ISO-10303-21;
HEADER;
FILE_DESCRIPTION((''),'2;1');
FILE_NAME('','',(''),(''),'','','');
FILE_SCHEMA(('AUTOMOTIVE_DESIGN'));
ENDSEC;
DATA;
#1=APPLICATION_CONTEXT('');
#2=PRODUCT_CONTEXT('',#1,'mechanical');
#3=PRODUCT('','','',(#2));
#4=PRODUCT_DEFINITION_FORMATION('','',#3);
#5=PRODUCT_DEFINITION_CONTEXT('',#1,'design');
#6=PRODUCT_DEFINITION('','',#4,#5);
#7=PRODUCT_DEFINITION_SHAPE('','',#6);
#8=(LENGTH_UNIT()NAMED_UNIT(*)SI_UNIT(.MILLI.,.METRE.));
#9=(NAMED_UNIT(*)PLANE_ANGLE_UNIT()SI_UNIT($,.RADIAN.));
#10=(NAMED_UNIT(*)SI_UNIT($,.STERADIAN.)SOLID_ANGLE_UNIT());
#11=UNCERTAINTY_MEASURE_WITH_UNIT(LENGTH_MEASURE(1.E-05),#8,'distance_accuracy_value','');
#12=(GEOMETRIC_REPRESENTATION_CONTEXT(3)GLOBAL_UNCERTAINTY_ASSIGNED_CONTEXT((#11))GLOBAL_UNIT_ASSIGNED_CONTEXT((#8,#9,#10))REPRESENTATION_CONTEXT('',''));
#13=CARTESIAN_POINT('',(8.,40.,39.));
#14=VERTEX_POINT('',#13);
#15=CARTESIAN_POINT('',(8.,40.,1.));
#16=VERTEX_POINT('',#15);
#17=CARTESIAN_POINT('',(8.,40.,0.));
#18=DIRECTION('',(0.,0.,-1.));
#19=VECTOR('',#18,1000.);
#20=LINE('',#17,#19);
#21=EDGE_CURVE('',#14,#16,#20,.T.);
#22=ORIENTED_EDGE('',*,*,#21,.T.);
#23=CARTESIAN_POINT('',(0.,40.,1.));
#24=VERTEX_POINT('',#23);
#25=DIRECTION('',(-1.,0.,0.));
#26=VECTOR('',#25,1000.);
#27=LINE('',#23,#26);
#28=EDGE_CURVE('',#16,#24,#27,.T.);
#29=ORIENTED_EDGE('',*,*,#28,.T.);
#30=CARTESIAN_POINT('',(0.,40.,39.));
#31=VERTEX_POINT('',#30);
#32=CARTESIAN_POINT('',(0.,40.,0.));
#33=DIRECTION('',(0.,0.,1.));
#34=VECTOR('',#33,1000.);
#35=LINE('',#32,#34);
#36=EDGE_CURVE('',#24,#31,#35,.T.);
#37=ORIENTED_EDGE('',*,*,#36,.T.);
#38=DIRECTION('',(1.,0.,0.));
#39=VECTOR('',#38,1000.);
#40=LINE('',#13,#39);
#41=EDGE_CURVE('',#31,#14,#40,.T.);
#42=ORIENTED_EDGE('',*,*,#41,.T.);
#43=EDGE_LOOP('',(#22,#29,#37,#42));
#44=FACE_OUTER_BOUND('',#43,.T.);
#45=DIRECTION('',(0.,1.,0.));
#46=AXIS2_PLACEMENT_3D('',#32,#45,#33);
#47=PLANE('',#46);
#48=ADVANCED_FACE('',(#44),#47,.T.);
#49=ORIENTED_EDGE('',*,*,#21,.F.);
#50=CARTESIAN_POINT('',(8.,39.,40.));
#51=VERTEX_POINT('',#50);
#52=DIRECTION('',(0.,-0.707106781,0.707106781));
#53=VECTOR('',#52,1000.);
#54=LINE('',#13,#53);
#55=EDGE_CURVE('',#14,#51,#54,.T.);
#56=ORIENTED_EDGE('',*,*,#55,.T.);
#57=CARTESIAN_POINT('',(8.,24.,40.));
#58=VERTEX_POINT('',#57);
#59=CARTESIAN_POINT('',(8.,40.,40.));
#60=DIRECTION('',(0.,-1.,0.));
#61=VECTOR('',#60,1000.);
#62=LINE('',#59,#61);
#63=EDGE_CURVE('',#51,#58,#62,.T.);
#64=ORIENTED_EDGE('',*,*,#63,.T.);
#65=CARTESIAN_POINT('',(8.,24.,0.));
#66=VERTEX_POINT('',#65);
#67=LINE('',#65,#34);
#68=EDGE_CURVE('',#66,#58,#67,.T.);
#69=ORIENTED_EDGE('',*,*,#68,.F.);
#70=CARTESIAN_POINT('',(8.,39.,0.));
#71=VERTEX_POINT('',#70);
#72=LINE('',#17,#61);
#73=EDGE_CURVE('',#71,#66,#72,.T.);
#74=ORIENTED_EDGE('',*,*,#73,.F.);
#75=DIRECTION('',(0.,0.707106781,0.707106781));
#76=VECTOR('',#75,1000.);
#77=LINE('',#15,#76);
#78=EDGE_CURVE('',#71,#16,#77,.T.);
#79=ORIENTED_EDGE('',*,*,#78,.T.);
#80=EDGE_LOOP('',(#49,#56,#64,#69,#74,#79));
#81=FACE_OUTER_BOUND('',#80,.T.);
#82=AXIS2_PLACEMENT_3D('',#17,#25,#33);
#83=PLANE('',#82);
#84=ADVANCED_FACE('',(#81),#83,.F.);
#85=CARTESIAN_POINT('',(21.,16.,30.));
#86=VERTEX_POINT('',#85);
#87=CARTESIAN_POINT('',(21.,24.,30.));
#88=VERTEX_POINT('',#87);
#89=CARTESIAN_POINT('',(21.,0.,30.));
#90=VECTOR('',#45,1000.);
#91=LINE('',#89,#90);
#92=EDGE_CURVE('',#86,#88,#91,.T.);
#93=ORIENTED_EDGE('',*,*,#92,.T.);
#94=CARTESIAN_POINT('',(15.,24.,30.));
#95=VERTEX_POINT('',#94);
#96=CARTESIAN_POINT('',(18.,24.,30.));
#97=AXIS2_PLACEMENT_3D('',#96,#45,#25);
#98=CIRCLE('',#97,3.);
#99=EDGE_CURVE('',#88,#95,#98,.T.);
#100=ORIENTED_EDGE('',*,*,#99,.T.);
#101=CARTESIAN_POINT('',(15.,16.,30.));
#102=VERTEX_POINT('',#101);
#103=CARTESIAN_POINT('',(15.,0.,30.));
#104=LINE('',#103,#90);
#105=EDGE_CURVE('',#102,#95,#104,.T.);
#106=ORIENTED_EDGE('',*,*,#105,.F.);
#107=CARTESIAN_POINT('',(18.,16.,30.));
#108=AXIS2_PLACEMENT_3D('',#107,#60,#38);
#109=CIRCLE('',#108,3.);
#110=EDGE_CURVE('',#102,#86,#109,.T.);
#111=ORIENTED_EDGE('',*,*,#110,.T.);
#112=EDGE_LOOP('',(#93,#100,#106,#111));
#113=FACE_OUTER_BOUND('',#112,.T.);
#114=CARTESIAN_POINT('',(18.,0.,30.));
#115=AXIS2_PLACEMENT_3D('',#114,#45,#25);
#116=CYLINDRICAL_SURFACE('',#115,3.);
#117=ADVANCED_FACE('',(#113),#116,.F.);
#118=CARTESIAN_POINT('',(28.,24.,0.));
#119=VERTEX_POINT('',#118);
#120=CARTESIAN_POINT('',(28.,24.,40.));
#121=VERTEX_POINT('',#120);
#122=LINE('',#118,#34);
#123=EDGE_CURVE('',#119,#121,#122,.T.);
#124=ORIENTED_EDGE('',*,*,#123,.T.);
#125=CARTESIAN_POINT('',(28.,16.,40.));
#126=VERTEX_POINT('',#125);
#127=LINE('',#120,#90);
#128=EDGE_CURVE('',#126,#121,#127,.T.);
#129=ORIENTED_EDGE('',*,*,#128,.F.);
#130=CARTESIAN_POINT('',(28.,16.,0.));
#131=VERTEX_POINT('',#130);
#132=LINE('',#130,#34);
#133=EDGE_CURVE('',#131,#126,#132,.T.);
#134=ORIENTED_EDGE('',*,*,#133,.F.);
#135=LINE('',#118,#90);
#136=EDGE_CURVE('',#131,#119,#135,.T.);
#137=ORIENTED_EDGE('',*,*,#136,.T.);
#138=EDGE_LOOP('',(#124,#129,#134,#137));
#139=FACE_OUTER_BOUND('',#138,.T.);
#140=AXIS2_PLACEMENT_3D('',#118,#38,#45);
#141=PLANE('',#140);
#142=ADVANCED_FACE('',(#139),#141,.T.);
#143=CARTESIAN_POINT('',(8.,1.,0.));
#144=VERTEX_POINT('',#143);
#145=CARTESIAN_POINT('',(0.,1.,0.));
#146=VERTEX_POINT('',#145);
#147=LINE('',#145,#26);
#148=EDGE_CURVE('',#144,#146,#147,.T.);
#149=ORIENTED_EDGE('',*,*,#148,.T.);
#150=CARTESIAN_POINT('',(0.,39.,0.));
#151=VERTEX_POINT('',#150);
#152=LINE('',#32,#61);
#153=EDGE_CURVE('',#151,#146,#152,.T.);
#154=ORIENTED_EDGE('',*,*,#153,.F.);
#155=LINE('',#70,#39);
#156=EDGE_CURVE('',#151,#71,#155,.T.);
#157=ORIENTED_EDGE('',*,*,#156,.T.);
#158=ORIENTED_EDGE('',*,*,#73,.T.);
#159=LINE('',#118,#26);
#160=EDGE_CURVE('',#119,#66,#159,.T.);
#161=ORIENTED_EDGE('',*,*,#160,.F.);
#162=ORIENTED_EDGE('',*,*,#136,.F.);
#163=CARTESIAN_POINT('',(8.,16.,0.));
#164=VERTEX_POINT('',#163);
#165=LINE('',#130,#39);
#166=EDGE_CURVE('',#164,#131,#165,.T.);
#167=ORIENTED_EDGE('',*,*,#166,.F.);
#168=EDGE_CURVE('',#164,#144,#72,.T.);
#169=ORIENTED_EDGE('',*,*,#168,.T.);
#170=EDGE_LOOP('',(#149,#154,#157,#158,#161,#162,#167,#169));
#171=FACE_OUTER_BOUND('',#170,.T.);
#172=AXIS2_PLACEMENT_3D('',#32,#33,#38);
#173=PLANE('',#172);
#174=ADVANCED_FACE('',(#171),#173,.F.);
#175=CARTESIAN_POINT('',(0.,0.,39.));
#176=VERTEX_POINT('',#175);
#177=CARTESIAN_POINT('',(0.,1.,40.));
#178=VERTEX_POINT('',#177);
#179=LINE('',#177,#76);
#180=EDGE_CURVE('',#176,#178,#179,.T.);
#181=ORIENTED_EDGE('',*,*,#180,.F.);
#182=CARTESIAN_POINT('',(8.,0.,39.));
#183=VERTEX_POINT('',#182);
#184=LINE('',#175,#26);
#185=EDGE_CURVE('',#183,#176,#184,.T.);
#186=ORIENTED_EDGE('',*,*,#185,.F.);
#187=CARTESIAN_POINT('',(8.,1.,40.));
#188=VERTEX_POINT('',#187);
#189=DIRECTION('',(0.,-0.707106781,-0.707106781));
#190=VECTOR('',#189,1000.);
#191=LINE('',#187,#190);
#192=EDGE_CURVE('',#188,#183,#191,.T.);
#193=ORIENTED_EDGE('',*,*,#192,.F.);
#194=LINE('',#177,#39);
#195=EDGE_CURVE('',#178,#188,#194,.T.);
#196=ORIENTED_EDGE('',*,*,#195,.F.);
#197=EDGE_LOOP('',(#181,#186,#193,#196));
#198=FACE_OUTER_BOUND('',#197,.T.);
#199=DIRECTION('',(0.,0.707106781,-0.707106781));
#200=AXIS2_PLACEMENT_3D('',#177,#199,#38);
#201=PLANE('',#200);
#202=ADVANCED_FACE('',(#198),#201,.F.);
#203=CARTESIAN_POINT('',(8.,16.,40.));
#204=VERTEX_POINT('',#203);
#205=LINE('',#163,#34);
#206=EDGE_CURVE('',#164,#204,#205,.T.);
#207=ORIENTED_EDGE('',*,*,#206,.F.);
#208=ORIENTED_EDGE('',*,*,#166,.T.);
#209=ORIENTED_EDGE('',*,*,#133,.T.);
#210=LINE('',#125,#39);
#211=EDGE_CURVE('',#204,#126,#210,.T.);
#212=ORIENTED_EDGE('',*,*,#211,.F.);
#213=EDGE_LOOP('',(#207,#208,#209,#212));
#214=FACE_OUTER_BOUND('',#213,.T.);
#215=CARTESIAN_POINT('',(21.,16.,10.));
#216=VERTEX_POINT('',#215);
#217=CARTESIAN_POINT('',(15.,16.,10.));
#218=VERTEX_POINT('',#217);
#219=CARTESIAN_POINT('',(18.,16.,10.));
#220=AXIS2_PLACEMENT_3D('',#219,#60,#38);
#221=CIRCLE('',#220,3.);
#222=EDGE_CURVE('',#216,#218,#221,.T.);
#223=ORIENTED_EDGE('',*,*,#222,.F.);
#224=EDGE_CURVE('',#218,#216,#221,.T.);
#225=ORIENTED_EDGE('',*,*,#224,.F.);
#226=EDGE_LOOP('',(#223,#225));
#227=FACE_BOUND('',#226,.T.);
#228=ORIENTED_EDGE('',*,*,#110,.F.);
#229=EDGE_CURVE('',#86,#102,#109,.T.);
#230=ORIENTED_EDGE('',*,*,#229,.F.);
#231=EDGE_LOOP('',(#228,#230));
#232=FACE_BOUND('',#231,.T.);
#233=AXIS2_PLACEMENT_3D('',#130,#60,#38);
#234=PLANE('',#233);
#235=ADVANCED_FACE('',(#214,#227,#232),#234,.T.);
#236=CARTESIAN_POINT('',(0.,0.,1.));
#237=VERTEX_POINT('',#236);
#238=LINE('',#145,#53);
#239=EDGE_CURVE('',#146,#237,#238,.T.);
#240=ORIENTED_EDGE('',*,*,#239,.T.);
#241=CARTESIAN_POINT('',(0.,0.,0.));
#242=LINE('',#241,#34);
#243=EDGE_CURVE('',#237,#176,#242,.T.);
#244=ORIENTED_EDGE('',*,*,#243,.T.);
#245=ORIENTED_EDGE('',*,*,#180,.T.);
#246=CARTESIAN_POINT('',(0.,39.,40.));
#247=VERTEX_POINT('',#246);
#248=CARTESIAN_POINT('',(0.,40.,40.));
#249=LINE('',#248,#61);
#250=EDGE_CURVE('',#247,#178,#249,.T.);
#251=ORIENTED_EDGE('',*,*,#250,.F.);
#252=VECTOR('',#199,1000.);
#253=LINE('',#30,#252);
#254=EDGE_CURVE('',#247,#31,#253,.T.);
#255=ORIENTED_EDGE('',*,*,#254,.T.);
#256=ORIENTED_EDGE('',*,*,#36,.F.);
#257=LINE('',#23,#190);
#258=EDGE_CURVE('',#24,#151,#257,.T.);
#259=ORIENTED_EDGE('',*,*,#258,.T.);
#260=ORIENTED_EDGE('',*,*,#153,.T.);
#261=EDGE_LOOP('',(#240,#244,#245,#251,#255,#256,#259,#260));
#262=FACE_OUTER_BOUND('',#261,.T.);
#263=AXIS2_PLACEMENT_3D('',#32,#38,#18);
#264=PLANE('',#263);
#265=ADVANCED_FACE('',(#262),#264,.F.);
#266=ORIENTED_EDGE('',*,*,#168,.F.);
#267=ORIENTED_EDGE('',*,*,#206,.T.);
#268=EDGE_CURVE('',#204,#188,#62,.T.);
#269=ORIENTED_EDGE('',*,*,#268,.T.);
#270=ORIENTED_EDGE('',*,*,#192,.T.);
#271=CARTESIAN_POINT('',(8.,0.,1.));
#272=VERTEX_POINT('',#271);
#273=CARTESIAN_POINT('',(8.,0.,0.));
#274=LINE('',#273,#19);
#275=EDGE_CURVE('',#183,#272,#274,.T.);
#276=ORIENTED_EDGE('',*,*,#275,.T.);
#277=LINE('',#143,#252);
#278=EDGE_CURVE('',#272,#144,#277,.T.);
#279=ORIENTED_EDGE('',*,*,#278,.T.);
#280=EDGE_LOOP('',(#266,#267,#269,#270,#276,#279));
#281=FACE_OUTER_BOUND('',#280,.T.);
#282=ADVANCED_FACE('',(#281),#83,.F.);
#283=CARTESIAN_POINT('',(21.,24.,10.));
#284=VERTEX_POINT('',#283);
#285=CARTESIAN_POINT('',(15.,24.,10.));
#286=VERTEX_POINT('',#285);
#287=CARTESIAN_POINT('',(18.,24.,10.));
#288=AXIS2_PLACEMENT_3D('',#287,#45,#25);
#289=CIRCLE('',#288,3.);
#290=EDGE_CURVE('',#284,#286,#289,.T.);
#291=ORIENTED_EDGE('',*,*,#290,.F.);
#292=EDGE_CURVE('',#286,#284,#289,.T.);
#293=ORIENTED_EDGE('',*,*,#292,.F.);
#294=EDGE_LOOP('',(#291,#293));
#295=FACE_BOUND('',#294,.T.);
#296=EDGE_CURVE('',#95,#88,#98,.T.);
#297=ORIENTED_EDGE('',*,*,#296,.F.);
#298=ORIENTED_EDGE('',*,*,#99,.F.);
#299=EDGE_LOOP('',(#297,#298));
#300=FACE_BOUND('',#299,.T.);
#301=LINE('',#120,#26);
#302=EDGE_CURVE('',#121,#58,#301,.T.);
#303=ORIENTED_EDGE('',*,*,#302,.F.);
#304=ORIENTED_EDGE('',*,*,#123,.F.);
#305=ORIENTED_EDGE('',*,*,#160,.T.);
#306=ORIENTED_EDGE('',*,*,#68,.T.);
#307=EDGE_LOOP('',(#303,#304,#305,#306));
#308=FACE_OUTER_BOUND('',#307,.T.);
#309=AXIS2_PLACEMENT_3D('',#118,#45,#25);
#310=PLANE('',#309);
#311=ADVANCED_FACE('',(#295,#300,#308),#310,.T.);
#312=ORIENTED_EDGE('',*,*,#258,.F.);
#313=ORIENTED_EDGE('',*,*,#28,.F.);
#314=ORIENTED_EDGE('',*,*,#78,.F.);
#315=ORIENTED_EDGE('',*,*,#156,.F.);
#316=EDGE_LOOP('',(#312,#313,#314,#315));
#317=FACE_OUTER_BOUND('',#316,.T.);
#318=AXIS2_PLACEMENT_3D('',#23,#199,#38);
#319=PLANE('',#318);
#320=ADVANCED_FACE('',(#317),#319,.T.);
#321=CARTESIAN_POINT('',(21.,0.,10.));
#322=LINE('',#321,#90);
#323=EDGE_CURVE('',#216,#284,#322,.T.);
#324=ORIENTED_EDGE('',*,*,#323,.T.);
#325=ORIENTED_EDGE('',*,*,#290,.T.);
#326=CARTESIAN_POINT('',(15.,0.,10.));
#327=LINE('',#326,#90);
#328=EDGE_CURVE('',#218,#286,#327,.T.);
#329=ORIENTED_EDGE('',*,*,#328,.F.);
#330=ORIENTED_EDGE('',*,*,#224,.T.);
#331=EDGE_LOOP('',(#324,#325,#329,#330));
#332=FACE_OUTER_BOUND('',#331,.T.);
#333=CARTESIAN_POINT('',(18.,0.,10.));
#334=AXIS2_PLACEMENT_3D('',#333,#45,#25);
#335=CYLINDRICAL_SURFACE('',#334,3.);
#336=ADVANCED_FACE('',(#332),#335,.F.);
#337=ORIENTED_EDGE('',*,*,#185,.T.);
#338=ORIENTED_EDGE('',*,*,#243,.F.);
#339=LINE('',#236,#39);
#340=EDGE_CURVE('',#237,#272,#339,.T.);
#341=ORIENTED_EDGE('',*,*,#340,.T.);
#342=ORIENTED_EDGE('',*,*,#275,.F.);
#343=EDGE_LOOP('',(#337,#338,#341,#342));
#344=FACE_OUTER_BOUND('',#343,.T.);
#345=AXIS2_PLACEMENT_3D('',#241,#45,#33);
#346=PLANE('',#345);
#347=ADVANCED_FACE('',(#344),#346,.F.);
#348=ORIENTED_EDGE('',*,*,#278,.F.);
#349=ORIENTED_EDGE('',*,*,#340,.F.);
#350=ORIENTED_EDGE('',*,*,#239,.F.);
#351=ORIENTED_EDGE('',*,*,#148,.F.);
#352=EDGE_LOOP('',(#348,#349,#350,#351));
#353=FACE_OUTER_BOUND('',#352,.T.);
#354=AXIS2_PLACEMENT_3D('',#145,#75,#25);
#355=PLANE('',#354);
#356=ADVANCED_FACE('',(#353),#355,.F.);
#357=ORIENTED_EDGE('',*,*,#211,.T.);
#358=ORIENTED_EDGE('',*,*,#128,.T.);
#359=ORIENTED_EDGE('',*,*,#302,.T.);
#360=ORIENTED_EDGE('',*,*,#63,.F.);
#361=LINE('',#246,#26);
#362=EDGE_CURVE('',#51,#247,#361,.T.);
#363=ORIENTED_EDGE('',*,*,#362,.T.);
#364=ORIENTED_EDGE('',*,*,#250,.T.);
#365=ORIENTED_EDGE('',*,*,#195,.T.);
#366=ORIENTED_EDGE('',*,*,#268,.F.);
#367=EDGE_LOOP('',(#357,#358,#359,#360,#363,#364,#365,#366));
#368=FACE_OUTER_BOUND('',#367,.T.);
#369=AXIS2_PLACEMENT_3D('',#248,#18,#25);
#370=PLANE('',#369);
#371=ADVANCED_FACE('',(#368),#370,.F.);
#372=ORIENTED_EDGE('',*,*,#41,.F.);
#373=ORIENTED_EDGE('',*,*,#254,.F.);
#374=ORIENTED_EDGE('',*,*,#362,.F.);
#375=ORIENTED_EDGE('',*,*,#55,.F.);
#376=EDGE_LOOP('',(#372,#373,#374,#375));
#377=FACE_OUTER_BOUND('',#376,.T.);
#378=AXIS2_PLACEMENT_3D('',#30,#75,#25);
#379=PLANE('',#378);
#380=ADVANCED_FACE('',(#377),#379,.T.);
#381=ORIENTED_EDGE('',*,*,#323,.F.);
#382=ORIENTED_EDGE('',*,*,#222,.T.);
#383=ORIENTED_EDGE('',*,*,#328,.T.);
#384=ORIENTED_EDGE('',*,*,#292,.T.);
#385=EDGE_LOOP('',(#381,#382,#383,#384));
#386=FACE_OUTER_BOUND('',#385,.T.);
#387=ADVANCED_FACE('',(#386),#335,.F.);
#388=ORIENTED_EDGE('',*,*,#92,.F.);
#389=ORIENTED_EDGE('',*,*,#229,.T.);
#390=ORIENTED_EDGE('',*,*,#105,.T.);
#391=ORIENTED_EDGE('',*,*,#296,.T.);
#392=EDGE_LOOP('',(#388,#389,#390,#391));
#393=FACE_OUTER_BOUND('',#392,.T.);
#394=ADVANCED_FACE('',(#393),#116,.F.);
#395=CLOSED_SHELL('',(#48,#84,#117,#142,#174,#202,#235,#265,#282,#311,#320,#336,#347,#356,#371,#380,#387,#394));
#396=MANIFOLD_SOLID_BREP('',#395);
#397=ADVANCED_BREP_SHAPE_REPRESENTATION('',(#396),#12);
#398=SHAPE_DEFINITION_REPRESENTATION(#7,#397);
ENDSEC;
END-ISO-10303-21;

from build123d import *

# Parameters (mm, degrees)
SKETCH1_W               = 8
SKETCH1_H               = 40
BOSS_EXTRUDE1_DEPTH     = 40
CHAMFER1_SIZE           = 1
SKETCH2_W               = 20
SKETCH2_H               = 8
BOSS_EXTRUDE2_DEPTH     = 40
CUT_EXTRUDE1_DEPTH      = 55.405882035
CUT_EXTRUDE1_DEPTH_BACK = 55.405882035
SKETCH4_R               = 3


with BuildPart() as part:
    # Sketch1 → Boss-Extrude1 (new body)
    with BuildSketch(Plane(origin=(0, 0, 0), x_dir=(1, 0, 0), z_dir=(0, 1, 0))):
        with Locations((4, -20)):
            Rectangle(SKETCH1_W, SKETCH1_H)
    extrude(amount=BOSS_EXTRUDE1_DEPTH)

    # Chamfer1
    chamfer1_edges = [part.edges().sort_by_distance(p)[0] for p in [
        (4, 40, 0),
        (4, 0, 0),
        (4, 0, 40),
        (4, 40, 40),
    ]]
    chamfer(chamfer1_edges, length=CHAMFER1_SIZE)

    # Sketch2 → Boss-Extrude2 (add)
    with BuildSketch(Plane.XY.offset(40)):
        with Locations((18, 20)):
            Rectangle(SKETCH2_W, SKETCH2_H)
    extrude(amount=-BOSS_EXTRUDE2_DEPTH)

    # Sketch4 → Cut-Extrude1 (cut, two sides: drawn at the far end of the back side and taken through both)
    with BuildSketch(Plane(origin=(0, 24, 0), x_dir=(1, 0, 0), z_dir=(0, 1, 0)).offset(-CUT_EXTRUDE1_DEPTH_BACK)):
        with Locations(Location((18, -30, 0), (0, 0, 180))):
            Circle(SKETCH4_R)
        with Locations(Location((18, -10, 0), (0, 0, 180))):
            Circle(SKETCH4_R)
    extrude(amount=CUT_EXTRUDE1_DEPTH + CUT_EXTRUDE1_DEPTH_BACK, mode=Mode.SUBTRACT)


solid = part.part
